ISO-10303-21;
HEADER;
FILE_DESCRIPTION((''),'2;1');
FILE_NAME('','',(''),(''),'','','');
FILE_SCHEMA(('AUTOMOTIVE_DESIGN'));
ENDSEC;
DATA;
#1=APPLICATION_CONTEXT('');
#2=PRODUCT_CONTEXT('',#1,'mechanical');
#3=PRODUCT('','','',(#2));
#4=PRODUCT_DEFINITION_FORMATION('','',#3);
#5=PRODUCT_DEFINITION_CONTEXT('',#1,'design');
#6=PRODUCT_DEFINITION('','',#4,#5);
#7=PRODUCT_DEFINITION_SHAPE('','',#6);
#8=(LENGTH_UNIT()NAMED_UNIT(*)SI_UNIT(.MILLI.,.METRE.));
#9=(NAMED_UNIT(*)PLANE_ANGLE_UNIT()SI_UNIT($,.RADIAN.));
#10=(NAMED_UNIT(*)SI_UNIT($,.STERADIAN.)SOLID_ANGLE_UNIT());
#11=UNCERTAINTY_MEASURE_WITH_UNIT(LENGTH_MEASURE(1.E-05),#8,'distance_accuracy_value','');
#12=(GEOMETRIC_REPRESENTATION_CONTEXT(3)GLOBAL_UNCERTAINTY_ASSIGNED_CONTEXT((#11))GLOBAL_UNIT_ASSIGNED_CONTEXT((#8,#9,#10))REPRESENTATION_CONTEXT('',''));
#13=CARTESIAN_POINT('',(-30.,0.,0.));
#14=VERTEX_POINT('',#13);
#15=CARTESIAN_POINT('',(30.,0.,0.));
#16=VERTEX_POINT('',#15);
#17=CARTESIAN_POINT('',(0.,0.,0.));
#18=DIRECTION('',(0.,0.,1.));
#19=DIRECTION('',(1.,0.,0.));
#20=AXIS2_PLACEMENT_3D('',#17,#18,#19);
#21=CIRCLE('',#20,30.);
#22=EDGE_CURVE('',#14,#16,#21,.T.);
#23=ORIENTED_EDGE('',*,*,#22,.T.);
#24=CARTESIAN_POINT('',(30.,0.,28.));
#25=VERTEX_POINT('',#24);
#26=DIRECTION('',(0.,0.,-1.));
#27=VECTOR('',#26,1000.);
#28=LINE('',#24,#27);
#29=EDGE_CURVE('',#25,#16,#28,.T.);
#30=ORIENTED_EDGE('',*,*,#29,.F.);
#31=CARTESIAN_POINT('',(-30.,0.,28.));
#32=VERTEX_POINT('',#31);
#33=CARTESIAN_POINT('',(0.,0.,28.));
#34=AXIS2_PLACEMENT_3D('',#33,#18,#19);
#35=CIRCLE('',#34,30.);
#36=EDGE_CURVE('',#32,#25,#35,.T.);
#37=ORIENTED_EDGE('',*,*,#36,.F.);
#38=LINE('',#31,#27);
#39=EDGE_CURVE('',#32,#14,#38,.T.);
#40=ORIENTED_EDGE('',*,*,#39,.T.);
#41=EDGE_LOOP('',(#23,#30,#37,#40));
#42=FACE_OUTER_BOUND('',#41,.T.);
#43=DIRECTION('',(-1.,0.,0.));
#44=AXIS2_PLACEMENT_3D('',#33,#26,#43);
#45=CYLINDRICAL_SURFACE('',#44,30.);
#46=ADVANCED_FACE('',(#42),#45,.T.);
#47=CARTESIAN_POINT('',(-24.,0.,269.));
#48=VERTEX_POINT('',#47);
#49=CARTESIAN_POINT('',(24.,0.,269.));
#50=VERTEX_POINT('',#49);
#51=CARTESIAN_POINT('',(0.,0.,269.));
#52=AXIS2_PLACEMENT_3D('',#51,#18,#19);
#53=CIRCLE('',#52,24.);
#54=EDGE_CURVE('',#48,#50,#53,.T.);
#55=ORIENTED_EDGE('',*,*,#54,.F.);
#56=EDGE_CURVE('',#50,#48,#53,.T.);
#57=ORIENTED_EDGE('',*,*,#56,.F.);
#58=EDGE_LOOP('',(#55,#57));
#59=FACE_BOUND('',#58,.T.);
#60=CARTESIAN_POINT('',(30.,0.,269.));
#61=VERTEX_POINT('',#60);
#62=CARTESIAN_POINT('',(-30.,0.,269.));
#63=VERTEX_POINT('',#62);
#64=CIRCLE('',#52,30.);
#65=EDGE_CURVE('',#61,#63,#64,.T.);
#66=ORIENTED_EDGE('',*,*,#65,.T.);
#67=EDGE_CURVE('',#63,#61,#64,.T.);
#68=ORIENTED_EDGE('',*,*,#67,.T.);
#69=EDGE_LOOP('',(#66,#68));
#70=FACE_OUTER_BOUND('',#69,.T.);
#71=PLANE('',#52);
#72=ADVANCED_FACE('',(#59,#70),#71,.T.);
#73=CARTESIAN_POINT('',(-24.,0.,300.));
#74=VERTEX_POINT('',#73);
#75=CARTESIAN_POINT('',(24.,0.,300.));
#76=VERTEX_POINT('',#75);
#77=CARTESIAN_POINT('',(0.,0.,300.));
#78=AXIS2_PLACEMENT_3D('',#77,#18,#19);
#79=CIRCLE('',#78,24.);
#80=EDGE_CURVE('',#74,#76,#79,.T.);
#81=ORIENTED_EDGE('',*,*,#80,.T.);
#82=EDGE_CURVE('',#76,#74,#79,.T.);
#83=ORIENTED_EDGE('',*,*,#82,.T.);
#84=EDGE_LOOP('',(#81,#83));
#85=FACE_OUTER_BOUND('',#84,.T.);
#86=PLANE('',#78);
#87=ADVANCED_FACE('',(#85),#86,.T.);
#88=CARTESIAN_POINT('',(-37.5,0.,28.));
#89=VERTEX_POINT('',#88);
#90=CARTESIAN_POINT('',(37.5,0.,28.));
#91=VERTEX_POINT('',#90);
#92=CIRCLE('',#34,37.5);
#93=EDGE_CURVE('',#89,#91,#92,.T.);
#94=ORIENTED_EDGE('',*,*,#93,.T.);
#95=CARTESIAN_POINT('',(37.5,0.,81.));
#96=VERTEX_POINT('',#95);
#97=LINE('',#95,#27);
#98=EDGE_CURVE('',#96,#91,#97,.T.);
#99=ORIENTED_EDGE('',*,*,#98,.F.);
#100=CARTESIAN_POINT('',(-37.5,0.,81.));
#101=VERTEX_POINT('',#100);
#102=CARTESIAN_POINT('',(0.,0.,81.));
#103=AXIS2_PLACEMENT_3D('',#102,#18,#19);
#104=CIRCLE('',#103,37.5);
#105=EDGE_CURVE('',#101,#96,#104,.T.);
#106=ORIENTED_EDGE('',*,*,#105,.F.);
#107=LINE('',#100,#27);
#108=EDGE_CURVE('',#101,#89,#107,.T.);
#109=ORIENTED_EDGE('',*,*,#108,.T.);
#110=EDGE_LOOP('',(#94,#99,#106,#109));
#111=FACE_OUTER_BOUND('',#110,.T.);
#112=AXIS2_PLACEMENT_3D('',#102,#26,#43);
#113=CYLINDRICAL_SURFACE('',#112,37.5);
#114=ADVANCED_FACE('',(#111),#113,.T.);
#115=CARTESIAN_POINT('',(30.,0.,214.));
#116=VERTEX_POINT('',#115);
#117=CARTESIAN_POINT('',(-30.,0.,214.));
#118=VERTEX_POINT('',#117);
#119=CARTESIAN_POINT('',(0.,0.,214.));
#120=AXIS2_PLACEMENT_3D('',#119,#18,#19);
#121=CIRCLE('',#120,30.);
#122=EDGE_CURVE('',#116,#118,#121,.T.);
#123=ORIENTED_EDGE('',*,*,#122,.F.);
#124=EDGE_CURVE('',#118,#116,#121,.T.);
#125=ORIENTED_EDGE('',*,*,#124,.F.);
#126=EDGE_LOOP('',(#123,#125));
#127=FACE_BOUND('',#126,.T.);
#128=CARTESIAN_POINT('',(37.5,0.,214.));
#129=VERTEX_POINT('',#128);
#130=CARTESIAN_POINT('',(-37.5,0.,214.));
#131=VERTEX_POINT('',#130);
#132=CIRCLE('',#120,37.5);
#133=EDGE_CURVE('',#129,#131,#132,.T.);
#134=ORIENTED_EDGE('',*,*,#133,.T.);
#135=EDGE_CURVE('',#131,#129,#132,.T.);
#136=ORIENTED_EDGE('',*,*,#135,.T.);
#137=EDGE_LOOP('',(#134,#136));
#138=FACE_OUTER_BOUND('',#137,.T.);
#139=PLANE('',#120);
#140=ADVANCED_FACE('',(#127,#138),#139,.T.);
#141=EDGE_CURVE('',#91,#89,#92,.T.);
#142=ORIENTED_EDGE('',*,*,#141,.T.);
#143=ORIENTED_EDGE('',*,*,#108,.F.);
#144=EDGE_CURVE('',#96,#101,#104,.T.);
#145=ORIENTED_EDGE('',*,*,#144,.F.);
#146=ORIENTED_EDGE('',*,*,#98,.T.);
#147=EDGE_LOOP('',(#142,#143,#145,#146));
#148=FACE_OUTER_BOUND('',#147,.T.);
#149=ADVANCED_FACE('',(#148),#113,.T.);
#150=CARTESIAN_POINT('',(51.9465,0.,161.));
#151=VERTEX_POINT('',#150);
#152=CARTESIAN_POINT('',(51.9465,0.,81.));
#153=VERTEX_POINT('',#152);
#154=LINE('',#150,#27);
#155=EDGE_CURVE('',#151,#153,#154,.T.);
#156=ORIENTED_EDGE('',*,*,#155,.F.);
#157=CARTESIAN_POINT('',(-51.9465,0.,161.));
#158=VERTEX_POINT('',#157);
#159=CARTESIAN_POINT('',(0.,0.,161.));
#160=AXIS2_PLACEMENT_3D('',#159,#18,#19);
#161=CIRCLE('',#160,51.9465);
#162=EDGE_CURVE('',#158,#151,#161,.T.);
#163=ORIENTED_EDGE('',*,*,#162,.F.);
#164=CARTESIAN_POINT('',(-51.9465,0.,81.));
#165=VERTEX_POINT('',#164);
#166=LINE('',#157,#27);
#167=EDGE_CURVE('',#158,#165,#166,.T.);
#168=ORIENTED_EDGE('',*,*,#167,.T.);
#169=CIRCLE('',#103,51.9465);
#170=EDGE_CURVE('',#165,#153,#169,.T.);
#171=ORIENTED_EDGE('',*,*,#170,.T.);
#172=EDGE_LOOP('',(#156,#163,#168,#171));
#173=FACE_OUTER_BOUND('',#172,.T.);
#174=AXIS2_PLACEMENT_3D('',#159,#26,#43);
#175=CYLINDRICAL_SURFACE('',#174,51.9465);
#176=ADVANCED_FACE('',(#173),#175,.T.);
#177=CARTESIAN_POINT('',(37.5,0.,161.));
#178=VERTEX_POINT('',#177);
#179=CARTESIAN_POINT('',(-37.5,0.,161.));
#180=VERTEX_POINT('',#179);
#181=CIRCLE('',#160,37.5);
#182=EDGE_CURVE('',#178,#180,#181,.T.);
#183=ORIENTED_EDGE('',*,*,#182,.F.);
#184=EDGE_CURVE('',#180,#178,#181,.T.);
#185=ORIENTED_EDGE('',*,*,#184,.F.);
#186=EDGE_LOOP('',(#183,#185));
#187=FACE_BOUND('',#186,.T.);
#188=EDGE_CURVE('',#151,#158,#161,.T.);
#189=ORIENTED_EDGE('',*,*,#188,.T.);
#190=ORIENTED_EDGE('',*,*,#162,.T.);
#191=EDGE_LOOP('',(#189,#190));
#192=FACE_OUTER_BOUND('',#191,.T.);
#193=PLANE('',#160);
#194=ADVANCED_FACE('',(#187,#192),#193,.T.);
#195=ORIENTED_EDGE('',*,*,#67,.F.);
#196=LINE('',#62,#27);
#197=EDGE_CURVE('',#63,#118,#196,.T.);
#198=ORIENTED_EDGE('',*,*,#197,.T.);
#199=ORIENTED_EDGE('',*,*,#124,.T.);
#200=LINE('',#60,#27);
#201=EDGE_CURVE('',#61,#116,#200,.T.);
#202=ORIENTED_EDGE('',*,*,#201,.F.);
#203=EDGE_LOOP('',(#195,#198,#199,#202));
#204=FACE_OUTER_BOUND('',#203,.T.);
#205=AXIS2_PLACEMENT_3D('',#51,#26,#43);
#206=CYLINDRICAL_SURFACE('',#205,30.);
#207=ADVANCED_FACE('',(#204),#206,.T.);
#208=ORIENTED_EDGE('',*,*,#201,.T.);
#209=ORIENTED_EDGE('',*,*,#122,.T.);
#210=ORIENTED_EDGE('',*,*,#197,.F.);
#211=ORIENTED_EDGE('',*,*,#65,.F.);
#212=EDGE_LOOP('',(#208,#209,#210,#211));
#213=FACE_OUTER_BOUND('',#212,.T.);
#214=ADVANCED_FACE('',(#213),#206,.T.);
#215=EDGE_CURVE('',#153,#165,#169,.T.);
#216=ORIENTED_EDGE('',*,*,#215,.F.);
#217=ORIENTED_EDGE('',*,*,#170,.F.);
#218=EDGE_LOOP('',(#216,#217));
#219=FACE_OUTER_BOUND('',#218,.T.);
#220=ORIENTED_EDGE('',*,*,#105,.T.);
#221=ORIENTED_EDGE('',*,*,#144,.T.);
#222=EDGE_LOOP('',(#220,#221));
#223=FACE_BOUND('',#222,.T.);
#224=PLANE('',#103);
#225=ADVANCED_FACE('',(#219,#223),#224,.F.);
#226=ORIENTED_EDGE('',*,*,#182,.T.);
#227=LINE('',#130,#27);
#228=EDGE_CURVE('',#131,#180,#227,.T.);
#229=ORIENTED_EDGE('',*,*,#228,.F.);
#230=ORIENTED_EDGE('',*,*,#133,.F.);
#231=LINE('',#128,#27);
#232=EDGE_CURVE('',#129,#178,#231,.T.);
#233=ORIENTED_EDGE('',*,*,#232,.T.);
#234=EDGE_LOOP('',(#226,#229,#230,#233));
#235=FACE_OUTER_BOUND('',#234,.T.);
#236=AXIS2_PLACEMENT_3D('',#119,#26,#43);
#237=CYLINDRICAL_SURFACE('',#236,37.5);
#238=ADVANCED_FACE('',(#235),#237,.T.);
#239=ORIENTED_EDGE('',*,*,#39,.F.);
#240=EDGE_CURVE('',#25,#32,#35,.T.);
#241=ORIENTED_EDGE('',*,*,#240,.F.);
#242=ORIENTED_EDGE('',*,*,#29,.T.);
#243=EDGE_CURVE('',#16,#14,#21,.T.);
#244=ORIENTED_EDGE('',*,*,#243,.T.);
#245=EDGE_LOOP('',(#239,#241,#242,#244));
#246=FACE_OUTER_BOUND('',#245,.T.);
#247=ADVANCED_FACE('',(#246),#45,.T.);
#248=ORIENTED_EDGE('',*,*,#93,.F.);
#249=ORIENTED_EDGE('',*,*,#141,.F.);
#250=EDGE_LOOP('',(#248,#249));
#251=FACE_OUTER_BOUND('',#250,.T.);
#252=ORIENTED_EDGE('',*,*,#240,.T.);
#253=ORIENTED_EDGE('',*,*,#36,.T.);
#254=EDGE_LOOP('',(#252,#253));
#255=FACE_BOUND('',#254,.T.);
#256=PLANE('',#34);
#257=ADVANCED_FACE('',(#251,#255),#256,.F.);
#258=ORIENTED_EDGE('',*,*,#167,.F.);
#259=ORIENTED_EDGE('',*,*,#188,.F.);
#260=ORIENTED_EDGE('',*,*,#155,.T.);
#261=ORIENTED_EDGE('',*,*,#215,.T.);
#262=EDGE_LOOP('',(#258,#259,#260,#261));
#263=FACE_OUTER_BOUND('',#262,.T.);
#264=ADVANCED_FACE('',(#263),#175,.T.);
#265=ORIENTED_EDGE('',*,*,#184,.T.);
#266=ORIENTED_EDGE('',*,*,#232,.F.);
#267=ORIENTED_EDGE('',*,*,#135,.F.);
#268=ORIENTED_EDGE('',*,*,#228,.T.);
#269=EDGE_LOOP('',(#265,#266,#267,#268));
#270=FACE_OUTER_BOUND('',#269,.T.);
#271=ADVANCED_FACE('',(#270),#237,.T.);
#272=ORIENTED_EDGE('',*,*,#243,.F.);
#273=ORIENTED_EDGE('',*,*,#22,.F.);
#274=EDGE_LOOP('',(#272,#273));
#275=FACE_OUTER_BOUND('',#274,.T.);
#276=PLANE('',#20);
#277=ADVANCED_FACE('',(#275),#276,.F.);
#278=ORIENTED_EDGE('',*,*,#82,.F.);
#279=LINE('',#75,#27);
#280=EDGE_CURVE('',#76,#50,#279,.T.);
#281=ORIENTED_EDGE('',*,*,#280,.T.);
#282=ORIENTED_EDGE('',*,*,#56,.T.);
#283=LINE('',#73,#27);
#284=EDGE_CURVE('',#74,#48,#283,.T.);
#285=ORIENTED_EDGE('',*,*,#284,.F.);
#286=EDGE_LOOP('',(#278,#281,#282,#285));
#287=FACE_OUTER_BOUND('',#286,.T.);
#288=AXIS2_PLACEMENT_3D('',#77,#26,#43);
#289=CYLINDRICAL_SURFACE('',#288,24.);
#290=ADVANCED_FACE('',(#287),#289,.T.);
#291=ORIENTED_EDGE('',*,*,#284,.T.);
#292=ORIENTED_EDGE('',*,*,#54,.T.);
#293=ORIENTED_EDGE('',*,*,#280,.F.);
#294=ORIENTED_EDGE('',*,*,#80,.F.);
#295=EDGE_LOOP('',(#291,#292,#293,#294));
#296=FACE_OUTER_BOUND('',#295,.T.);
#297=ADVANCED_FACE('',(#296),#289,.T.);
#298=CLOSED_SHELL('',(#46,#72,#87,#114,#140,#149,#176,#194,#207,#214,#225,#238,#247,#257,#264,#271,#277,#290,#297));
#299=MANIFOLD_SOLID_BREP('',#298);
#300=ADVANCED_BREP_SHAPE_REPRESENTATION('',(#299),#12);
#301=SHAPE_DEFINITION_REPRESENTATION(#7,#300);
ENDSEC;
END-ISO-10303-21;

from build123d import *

# Parameters (mm, degrees)
SKETCH1_R           = 30
BOSS_EXTRUDE1_DEPTH = 28
SKETCH2_R           = 37.5
BOSS_EXTRUDE2_DEPTH = 53
SKETCH3_R           = 51.9465
BOSS_EXTRUDE3_DEPTH = 80
SKETCH4_R           = 37.5
BOSS_EXTRUDE4_DEPTH = 53
SKETCH5_R           = 30
BOSS_EXTRUDE5_DEPTH = 55
SKETCH6_R           = 24
BOSS_EXTRUDE6_DEPTH = 31


with BuildPart() as part:
    # Sketch1 → Boss-Extrude1 (new body)
    with BuildSketch(Plane.XY):
        Circle(SKETCH1_R)
    extrude(amount=BOSS_EXTRUDE1_DEPTH)

    # Sketch2 → Boss-Extrude2 (add)
    with BuildSketch(Plane.XY.offset(28)):
        Circle(SKETCH2_R)
    extrude(amount=BOSS_EXTRUDE2_DEPTH)

    # Sketch3 → Boss-Extrude3 (add)
    with BuildSketch(Plane.XY.offset(81)):
        Circle(SKETCH3_R)
    extrude(amount=BOSS_EXTRUDE3_DEPTH)

    # Sketch4 → Boss-Extrude4 (add)
    with BuildSketch(Plane.XY.offset(161)):
        Circle(SKETCH4_R)
    extrude(amount=BOSS_EXTRUDE4_DEPTH)

    # Sketch5 → Boss-Extrude5 (add)
    with BuildSketch(Plane.XY.offset(214)):
        Circle(SKETCH5_R)
    extrude(amount=BOSS_EXTRUDE5_DEPTH)

    # Sketch6 → Boss-Extrude6 (add)
    with BuildSketch(Plane.XY.offset(269)):
        Circle(SKETCH6_R)
    extrude(amount=BOSS_EXTRUDE6_DEPTH)


solid = part.part
